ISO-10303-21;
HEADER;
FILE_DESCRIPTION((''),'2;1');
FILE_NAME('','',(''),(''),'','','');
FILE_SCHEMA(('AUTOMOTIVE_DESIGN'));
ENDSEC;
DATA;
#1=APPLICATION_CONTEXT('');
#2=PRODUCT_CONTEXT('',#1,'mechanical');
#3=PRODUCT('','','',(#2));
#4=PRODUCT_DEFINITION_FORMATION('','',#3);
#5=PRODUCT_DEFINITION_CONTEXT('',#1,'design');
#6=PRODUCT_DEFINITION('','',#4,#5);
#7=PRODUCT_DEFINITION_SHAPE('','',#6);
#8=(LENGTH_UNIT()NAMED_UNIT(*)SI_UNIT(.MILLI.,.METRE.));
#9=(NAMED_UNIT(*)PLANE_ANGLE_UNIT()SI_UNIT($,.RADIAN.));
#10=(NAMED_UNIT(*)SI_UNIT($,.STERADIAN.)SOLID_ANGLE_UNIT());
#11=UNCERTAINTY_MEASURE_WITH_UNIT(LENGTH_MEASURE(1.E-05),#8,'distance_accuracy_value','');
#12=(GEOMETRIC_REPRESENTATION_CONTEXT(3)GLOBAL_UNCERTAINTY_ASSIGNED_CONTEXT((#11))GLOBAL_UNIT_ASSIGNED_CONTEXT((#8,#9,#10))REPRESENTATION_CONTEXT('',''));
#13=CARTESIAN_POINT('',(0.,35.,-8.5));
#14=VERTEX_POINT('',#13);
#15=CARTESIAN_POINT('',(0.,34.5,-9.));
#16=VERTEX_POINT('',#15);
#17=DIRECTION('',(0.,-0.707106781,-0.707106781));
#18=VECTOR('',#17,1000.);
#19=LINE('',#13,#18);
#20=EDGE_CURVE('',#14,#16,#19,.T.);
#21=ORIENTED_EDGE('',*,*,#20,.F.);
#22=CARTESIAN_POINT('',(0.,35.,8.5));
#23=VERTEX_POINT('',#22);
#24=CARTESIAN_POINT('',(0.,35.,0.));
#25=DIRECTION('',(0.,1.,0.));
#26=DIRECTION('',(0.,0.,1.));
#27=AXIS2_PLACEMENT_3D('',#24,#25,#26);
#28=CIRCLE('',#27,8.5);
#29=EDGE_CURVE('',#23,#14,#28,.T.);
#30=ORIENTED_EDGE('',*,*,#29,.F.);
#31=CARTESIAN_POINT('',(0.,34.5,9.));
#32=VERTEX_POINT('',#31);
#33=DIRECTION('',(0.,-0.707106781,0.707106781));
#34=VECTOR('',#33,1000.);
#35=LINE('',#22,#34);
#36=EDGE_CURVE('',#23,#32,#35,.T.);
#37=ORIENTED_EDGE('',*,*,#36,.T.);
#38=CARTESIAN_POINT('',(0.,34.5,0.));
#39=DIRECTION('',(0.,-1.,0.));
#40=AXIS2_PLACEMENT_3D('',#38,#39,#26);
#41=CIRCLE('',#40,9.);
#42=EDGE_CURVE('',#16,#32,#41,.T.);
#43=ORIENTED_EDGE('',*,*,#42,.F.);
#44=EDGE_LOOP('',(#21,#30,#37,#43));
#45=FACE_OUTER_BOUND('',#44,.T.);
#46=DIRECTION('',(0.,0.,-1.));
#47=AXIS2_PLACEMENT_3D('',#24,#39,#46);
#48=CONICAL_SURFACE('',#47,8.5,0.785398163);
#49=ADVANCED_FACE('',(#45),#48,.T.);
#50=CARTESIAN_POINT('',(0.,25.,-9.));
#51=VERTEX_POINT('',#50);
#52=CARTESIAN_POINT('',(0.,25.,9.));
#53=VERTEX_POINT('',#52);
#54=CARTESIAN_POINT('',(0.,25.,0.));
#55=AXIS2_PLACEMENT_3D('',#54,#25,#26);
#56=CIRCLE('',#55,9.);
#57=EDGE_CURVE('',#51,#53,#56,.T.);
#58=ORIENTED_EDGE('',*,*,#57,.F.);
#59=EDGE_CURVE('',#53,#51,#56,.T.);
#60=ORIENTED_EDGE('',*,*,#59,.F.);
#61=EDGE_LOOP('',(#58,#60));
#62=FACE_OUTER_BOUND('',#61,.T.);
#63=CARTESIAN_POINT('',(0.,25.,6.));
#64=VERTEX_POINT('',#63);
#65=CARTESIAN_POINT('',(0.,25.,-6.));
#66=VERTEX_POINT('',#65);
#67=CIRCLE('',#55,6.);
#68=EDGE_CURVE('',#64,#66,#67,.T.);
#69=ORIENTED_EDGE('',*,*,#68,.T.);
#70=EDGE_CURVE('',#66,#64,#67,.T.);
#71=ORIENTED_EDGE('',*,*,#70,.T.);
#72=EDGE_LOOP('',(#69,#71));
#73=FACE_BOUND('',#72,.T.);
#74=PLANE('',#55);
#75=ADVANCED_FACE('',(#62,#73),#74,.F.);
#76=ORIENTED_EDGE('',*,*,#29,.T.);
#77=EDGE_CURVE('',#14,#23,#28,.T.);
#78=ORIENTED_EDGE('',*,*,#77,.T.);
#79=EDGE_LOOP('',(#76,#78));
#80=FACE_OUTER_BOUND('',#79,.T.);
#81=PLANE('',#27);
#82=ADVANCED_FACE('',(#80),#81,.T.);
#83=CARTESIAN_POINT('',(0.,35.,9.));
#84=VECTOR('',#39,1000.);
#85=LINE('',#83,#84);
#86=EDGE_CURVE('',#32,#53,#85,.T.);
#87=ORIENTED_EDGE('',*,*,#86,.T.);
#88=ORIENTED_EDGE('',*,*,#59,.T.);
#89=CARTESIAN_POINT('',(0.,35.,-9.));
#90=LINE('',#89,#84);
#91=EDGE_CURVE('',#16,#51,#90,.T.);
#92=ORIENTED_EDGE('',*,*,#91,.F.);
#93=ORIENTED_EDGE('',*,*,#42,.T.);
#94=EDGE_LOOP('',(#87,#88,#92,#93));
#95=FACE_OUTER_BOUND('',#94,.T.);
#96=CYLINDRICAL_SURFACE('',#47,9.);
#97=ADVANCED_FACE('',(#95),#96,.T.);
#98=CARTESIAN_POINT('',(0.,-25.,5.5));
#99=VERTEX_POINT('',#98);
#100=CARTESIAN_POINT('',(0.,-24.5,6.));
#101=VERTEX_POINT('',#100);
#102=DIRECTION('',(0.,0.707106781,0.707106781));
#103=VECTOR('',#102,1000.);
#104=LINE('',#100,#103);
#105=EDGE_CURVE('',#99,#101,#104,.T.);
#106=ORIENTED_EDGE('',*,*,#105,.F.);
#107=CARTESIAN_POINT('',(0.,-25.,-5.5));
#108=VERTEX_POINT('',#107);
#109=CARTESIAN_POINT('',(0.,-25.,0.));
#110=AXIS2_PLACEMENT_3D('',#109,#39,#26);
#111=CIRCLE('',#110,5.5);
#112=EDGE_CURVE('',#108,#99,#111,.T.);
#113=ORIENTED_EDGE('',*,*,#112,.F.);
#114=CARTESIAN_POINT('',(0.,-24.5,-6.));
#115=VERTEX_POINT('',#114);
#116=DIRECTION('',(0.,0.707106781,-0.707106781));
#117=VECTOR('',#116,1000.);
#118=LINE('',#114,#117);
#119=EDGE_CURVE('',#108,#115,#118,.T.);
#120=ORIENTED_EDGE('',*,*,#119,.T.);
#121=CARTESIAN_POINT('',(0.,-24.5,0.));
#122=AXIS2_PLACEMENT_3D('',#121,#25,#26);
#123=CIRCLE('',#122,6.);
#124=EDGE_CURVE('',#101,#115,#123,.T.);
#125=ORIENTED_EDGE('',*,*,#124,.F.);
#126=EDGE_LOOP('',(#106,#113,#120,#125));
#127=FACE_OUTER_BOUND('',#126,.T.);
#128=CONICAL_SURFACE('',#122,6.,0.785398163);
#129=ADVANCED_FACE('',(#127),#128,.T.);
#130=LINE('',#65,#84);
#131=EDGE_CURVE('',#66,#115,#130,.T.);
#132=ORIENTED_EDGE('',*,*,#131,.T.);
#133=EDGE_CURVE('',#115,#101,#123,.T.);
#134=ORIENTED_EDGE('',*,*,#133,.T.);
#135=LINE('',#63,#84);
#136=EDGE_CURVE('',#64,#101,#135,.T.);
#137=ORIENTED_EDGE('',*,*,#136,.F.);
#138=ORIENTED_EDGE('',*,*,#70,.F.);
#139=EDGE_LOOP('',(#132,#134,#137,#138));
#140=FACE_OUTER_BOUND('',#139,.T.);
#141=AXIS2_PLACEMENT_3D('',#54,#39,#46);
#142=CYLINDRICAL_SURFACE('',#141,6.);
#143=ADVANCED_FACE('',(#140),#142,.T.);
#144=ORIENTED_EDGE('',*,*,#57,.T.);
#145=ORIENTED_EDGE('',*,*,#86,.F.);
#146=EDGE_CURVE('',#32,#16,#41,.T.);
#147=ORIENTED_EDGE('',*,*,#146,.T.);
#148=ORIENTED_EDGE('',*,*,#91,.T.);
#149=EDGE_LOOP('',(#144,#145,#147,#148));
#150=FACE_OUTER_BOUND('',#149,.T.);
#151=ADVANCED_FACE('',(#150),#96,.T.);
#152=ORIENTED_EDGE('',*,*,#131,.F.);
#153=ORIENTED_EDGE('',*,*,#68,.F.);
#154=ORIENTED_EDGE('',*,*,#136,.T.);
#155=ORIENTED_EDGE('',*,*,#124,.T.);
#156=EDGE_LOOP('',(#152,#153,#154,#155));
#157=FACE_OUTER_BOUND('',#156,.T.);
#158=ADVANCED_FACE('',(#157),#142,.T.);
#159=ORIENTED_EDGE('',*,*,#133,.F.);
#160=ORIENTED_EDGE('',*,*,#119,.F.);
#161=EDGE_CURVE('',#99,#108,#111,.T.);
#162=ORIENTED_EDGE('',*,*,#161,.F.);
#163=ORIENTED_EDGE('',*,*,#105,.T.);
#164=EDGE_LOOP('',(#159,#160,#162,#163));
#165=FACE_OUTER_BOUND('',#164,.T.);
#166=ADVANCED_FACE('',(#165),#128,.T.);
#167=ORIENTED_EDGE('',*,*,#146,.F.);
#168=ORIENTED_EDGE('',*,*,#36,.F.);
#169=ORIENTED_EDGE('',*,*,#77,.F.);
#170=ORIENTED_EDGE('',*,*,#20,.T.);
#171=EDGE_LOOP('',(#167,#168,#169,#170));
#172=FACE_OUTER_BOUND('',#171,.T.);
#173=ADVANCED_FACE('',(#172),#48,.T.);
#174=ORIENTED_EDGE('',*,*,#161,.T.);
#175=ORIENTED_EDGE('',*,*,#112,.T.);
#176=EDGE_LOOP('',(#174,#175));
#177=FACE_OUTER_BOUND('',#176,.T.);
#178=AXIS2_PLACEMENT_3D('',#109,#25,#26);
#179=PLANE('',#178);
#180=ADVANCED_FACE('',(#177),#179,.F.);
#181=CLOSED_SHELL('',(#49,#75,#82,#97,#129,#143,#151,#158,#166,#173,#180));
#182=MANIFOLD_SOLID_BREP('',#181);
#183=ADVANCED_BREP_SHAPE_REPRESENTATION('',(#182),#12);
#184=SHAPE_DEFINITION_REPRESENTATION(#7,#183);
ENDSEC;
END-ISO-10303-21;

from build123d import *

# Parameters (mm, degrees)
SKETCH_1_R      = 6
EXTRUDE_1_DEPTH = 25
SKETCH_2_R      = 9
EXTRUDE_2_DEPTH = 10
CHAMFER_1_SIZE  = 0.5


with BuildPart() as part:
    # 草图1 → 凸台-拉伸1 (new, symmetric)
    with BuildSketch(Plane(origin=(0, 0, 0), x_dir=(1, 0, 0), z_dir=(0, 1, 0))):
        with Locations(Location((0, 0, 0), (0, 0, 270))):
            Circle(SKETCH_1_R)
    extrude(amount=EXTRUDE_1_DEPTH, both=True)

    # 草图2 → 凸台-拉伸2 (add)
    with BuildSketch(Plane(origin=(0, 25, 0), x_dir=(1, 0, 0), z_dir=(0, 1, 0))):
        with Locations(Location((0, 0, 0), (0, 0, 270))):
            Circle(SKETCH_2_R)
    extrude(amount=EXTRUDE_2_DEPTH)

    # 倒角1
    chamfer_1_edges = [part.edges().sort_by_distance(p)[0] for p in [
        (0, -25, -6),
        (0, 35, -9),
    ]]
    chamfer(chamfer_1_edges, length=CHAMFER_1_SIZE)


solid = part.part
